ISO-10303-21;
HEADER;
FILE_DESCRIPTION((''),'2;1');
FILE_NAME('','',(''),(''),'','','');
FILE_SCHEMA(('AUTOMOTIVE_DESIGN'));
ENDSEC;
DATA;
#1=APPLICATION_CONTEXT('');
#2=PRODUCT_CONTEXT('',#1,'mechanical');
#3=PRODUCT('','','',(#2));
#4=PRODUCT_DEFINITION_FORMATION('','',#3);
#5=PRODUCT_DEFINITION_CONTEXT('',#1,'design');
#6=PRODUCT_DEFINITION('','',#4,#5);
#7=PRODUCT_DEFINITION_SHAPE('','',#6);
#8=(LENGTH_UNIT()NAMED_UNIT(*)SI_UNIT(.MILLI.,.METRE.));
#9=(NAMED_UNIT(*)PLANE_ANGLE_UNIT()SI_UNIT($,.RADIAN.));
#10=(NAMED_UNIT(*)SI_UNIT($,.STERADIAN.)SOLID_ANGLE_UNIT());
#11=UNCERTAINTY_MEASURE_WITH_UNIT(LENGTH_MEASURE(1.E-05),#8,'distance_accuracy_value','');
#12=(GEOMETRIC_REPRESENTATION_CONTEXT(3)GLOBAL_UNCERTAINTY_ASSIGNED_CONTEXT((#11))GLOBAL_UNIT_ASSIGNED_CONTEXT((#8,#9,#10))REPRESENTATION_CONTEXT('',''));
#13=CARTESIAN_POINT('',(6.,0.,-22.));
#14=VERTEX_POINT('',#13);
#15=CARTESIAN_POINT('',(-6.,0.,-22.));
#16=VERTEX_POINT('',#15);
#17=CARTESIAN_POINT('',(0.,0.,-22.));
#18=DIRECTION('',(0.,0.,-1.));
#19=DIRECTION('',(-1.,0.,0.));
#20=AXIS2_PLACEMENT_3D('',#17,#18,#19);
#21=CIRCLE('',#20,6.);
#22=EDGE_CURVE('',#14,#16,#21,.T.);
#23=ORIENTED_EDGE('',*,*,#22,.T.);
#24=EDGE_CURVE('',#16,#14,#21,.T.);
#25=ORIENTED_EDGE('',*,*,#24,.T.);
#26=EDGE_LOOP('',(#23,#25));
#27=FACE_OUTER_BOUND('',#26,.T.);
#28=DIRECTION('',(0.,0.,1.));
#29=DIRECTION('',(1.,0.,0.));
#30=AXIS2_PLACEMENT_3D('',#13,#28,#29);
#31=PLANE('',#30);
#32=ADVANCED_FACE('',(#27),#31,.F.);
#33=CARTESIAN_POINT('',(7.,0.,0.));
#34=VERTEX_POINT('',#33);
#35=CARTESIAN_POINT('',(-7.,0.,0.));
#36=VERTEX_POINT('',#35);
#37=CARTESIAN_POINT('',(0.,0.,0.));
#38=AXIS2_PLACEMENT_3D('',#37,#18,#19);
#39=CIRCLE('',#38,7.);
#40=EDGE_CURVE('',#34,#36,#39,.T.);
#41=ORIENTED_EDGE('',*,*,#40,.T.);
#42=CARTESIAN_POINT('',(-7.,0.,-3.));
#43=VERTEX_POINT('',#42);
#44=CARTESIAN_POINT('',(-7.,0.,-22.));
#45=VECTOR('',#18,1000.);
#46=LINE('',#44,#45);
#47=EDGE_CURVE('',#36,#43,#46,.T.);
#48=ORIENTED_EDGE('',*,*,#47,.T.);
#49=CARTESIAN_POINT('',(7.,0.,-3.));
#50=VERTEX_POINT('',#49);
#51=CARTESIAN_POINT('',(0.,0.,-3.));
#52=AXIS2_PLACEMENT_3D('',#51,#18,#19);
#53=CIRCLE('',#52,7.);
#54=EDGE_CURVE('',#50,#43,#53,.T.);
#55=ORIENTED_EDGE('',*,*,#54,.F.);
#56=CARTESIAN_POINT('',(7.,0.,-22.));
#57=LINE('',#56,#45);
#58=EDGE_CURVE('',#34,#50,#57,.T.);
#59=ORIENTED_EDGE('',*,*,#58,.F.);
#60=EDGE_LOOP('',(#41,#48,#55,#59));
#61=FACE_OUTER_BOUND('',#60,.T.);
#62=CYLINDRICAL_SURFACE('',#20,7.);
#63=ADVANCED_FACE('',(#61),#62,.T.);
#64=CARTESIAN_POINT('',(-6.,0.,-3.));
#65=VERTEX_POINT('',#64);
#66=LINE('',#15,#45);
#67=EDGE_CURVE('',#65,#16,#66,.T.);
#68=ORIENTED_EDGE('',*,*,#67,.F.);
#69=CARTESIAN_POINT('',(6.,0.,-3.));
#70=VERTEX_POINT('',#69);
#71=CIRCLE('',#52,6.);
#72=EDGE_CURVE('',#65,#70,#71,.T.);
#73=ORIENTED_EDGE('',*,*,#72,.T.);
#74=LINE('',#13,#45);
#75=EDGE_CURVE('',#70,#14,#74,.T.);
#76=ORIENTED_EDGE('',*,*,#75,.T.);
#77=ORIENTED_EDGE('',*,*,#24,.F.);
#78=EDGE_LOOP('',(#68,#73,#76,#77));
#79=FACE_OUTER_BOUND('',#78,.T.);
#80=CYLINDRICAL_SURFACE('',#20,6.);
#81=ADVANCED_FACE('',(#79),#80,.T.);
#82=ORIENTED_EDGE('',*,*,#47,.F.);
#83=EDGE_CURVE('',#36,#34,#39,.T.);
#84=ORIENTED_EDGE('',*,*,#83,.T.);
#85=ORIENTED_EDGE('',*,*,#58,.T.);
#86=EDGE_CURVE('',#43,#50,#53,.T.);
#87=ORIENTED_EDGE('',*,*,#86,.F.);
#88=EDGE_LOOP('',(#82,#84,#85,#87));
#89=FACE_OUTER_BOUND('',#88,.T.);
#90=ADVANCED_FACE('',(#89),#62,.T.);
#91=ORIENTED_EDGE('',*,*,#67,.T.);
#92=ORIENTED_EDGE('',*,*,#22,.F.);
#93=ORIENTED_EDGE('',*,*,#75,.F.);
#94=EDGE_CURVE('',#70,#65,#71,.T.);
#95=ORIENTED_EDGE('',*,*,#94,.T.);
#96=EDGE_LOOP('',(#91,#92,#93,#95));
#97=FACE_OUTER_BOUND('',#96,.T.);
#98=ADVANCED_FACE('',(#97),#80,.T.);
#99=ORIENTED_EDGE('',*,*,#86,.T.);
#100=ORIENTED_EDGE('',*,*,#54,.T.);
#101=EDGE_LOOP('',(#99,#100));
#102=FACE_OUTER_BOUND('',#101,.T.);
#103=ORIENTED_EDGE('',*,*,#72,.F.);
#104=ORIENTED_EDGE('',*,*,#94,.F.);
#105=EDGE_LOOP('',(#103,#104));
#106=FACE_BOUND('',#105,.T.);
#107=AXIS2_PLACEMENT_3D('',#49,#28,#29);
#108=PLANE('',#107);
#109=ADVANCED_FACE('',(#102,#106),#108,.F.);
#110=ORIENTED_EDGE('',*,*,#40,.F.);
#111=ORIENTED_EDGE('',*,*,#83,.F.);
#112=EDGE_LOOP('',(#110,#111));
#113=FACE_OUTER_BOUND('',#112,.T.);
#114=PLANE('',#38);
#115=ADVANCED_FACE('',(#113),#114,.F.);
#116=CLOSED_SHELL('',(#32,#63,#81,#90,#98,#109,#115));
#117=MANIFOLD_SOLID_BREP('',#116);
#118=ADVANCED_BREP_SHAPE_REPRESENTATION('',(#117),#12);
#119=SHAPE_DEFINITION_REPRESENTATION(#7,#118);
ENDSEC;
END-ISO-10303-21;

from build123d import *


with BuildPart() as part:
    # Sketch1 → Revolve1 (revolve)
    with BuildSketch(Plane(origin=(0, 0, 0), x_dir=(1, 0, 0), z_dir=(0, 1, 0)), mode=Mode.PRIVATE) as revolve1_sk:
        Polygon((0, 0), (7, 0), (7, 3), (6, 3), (6, 22), (0, 22), align=None)
    revolve(revolve1_sk.sketch.rotate(Axis((0, 0, -22), (0, 0, 1)), 180), axis=Axis((0, 0, -22), (0, 0, 1)))


solid = part.part
